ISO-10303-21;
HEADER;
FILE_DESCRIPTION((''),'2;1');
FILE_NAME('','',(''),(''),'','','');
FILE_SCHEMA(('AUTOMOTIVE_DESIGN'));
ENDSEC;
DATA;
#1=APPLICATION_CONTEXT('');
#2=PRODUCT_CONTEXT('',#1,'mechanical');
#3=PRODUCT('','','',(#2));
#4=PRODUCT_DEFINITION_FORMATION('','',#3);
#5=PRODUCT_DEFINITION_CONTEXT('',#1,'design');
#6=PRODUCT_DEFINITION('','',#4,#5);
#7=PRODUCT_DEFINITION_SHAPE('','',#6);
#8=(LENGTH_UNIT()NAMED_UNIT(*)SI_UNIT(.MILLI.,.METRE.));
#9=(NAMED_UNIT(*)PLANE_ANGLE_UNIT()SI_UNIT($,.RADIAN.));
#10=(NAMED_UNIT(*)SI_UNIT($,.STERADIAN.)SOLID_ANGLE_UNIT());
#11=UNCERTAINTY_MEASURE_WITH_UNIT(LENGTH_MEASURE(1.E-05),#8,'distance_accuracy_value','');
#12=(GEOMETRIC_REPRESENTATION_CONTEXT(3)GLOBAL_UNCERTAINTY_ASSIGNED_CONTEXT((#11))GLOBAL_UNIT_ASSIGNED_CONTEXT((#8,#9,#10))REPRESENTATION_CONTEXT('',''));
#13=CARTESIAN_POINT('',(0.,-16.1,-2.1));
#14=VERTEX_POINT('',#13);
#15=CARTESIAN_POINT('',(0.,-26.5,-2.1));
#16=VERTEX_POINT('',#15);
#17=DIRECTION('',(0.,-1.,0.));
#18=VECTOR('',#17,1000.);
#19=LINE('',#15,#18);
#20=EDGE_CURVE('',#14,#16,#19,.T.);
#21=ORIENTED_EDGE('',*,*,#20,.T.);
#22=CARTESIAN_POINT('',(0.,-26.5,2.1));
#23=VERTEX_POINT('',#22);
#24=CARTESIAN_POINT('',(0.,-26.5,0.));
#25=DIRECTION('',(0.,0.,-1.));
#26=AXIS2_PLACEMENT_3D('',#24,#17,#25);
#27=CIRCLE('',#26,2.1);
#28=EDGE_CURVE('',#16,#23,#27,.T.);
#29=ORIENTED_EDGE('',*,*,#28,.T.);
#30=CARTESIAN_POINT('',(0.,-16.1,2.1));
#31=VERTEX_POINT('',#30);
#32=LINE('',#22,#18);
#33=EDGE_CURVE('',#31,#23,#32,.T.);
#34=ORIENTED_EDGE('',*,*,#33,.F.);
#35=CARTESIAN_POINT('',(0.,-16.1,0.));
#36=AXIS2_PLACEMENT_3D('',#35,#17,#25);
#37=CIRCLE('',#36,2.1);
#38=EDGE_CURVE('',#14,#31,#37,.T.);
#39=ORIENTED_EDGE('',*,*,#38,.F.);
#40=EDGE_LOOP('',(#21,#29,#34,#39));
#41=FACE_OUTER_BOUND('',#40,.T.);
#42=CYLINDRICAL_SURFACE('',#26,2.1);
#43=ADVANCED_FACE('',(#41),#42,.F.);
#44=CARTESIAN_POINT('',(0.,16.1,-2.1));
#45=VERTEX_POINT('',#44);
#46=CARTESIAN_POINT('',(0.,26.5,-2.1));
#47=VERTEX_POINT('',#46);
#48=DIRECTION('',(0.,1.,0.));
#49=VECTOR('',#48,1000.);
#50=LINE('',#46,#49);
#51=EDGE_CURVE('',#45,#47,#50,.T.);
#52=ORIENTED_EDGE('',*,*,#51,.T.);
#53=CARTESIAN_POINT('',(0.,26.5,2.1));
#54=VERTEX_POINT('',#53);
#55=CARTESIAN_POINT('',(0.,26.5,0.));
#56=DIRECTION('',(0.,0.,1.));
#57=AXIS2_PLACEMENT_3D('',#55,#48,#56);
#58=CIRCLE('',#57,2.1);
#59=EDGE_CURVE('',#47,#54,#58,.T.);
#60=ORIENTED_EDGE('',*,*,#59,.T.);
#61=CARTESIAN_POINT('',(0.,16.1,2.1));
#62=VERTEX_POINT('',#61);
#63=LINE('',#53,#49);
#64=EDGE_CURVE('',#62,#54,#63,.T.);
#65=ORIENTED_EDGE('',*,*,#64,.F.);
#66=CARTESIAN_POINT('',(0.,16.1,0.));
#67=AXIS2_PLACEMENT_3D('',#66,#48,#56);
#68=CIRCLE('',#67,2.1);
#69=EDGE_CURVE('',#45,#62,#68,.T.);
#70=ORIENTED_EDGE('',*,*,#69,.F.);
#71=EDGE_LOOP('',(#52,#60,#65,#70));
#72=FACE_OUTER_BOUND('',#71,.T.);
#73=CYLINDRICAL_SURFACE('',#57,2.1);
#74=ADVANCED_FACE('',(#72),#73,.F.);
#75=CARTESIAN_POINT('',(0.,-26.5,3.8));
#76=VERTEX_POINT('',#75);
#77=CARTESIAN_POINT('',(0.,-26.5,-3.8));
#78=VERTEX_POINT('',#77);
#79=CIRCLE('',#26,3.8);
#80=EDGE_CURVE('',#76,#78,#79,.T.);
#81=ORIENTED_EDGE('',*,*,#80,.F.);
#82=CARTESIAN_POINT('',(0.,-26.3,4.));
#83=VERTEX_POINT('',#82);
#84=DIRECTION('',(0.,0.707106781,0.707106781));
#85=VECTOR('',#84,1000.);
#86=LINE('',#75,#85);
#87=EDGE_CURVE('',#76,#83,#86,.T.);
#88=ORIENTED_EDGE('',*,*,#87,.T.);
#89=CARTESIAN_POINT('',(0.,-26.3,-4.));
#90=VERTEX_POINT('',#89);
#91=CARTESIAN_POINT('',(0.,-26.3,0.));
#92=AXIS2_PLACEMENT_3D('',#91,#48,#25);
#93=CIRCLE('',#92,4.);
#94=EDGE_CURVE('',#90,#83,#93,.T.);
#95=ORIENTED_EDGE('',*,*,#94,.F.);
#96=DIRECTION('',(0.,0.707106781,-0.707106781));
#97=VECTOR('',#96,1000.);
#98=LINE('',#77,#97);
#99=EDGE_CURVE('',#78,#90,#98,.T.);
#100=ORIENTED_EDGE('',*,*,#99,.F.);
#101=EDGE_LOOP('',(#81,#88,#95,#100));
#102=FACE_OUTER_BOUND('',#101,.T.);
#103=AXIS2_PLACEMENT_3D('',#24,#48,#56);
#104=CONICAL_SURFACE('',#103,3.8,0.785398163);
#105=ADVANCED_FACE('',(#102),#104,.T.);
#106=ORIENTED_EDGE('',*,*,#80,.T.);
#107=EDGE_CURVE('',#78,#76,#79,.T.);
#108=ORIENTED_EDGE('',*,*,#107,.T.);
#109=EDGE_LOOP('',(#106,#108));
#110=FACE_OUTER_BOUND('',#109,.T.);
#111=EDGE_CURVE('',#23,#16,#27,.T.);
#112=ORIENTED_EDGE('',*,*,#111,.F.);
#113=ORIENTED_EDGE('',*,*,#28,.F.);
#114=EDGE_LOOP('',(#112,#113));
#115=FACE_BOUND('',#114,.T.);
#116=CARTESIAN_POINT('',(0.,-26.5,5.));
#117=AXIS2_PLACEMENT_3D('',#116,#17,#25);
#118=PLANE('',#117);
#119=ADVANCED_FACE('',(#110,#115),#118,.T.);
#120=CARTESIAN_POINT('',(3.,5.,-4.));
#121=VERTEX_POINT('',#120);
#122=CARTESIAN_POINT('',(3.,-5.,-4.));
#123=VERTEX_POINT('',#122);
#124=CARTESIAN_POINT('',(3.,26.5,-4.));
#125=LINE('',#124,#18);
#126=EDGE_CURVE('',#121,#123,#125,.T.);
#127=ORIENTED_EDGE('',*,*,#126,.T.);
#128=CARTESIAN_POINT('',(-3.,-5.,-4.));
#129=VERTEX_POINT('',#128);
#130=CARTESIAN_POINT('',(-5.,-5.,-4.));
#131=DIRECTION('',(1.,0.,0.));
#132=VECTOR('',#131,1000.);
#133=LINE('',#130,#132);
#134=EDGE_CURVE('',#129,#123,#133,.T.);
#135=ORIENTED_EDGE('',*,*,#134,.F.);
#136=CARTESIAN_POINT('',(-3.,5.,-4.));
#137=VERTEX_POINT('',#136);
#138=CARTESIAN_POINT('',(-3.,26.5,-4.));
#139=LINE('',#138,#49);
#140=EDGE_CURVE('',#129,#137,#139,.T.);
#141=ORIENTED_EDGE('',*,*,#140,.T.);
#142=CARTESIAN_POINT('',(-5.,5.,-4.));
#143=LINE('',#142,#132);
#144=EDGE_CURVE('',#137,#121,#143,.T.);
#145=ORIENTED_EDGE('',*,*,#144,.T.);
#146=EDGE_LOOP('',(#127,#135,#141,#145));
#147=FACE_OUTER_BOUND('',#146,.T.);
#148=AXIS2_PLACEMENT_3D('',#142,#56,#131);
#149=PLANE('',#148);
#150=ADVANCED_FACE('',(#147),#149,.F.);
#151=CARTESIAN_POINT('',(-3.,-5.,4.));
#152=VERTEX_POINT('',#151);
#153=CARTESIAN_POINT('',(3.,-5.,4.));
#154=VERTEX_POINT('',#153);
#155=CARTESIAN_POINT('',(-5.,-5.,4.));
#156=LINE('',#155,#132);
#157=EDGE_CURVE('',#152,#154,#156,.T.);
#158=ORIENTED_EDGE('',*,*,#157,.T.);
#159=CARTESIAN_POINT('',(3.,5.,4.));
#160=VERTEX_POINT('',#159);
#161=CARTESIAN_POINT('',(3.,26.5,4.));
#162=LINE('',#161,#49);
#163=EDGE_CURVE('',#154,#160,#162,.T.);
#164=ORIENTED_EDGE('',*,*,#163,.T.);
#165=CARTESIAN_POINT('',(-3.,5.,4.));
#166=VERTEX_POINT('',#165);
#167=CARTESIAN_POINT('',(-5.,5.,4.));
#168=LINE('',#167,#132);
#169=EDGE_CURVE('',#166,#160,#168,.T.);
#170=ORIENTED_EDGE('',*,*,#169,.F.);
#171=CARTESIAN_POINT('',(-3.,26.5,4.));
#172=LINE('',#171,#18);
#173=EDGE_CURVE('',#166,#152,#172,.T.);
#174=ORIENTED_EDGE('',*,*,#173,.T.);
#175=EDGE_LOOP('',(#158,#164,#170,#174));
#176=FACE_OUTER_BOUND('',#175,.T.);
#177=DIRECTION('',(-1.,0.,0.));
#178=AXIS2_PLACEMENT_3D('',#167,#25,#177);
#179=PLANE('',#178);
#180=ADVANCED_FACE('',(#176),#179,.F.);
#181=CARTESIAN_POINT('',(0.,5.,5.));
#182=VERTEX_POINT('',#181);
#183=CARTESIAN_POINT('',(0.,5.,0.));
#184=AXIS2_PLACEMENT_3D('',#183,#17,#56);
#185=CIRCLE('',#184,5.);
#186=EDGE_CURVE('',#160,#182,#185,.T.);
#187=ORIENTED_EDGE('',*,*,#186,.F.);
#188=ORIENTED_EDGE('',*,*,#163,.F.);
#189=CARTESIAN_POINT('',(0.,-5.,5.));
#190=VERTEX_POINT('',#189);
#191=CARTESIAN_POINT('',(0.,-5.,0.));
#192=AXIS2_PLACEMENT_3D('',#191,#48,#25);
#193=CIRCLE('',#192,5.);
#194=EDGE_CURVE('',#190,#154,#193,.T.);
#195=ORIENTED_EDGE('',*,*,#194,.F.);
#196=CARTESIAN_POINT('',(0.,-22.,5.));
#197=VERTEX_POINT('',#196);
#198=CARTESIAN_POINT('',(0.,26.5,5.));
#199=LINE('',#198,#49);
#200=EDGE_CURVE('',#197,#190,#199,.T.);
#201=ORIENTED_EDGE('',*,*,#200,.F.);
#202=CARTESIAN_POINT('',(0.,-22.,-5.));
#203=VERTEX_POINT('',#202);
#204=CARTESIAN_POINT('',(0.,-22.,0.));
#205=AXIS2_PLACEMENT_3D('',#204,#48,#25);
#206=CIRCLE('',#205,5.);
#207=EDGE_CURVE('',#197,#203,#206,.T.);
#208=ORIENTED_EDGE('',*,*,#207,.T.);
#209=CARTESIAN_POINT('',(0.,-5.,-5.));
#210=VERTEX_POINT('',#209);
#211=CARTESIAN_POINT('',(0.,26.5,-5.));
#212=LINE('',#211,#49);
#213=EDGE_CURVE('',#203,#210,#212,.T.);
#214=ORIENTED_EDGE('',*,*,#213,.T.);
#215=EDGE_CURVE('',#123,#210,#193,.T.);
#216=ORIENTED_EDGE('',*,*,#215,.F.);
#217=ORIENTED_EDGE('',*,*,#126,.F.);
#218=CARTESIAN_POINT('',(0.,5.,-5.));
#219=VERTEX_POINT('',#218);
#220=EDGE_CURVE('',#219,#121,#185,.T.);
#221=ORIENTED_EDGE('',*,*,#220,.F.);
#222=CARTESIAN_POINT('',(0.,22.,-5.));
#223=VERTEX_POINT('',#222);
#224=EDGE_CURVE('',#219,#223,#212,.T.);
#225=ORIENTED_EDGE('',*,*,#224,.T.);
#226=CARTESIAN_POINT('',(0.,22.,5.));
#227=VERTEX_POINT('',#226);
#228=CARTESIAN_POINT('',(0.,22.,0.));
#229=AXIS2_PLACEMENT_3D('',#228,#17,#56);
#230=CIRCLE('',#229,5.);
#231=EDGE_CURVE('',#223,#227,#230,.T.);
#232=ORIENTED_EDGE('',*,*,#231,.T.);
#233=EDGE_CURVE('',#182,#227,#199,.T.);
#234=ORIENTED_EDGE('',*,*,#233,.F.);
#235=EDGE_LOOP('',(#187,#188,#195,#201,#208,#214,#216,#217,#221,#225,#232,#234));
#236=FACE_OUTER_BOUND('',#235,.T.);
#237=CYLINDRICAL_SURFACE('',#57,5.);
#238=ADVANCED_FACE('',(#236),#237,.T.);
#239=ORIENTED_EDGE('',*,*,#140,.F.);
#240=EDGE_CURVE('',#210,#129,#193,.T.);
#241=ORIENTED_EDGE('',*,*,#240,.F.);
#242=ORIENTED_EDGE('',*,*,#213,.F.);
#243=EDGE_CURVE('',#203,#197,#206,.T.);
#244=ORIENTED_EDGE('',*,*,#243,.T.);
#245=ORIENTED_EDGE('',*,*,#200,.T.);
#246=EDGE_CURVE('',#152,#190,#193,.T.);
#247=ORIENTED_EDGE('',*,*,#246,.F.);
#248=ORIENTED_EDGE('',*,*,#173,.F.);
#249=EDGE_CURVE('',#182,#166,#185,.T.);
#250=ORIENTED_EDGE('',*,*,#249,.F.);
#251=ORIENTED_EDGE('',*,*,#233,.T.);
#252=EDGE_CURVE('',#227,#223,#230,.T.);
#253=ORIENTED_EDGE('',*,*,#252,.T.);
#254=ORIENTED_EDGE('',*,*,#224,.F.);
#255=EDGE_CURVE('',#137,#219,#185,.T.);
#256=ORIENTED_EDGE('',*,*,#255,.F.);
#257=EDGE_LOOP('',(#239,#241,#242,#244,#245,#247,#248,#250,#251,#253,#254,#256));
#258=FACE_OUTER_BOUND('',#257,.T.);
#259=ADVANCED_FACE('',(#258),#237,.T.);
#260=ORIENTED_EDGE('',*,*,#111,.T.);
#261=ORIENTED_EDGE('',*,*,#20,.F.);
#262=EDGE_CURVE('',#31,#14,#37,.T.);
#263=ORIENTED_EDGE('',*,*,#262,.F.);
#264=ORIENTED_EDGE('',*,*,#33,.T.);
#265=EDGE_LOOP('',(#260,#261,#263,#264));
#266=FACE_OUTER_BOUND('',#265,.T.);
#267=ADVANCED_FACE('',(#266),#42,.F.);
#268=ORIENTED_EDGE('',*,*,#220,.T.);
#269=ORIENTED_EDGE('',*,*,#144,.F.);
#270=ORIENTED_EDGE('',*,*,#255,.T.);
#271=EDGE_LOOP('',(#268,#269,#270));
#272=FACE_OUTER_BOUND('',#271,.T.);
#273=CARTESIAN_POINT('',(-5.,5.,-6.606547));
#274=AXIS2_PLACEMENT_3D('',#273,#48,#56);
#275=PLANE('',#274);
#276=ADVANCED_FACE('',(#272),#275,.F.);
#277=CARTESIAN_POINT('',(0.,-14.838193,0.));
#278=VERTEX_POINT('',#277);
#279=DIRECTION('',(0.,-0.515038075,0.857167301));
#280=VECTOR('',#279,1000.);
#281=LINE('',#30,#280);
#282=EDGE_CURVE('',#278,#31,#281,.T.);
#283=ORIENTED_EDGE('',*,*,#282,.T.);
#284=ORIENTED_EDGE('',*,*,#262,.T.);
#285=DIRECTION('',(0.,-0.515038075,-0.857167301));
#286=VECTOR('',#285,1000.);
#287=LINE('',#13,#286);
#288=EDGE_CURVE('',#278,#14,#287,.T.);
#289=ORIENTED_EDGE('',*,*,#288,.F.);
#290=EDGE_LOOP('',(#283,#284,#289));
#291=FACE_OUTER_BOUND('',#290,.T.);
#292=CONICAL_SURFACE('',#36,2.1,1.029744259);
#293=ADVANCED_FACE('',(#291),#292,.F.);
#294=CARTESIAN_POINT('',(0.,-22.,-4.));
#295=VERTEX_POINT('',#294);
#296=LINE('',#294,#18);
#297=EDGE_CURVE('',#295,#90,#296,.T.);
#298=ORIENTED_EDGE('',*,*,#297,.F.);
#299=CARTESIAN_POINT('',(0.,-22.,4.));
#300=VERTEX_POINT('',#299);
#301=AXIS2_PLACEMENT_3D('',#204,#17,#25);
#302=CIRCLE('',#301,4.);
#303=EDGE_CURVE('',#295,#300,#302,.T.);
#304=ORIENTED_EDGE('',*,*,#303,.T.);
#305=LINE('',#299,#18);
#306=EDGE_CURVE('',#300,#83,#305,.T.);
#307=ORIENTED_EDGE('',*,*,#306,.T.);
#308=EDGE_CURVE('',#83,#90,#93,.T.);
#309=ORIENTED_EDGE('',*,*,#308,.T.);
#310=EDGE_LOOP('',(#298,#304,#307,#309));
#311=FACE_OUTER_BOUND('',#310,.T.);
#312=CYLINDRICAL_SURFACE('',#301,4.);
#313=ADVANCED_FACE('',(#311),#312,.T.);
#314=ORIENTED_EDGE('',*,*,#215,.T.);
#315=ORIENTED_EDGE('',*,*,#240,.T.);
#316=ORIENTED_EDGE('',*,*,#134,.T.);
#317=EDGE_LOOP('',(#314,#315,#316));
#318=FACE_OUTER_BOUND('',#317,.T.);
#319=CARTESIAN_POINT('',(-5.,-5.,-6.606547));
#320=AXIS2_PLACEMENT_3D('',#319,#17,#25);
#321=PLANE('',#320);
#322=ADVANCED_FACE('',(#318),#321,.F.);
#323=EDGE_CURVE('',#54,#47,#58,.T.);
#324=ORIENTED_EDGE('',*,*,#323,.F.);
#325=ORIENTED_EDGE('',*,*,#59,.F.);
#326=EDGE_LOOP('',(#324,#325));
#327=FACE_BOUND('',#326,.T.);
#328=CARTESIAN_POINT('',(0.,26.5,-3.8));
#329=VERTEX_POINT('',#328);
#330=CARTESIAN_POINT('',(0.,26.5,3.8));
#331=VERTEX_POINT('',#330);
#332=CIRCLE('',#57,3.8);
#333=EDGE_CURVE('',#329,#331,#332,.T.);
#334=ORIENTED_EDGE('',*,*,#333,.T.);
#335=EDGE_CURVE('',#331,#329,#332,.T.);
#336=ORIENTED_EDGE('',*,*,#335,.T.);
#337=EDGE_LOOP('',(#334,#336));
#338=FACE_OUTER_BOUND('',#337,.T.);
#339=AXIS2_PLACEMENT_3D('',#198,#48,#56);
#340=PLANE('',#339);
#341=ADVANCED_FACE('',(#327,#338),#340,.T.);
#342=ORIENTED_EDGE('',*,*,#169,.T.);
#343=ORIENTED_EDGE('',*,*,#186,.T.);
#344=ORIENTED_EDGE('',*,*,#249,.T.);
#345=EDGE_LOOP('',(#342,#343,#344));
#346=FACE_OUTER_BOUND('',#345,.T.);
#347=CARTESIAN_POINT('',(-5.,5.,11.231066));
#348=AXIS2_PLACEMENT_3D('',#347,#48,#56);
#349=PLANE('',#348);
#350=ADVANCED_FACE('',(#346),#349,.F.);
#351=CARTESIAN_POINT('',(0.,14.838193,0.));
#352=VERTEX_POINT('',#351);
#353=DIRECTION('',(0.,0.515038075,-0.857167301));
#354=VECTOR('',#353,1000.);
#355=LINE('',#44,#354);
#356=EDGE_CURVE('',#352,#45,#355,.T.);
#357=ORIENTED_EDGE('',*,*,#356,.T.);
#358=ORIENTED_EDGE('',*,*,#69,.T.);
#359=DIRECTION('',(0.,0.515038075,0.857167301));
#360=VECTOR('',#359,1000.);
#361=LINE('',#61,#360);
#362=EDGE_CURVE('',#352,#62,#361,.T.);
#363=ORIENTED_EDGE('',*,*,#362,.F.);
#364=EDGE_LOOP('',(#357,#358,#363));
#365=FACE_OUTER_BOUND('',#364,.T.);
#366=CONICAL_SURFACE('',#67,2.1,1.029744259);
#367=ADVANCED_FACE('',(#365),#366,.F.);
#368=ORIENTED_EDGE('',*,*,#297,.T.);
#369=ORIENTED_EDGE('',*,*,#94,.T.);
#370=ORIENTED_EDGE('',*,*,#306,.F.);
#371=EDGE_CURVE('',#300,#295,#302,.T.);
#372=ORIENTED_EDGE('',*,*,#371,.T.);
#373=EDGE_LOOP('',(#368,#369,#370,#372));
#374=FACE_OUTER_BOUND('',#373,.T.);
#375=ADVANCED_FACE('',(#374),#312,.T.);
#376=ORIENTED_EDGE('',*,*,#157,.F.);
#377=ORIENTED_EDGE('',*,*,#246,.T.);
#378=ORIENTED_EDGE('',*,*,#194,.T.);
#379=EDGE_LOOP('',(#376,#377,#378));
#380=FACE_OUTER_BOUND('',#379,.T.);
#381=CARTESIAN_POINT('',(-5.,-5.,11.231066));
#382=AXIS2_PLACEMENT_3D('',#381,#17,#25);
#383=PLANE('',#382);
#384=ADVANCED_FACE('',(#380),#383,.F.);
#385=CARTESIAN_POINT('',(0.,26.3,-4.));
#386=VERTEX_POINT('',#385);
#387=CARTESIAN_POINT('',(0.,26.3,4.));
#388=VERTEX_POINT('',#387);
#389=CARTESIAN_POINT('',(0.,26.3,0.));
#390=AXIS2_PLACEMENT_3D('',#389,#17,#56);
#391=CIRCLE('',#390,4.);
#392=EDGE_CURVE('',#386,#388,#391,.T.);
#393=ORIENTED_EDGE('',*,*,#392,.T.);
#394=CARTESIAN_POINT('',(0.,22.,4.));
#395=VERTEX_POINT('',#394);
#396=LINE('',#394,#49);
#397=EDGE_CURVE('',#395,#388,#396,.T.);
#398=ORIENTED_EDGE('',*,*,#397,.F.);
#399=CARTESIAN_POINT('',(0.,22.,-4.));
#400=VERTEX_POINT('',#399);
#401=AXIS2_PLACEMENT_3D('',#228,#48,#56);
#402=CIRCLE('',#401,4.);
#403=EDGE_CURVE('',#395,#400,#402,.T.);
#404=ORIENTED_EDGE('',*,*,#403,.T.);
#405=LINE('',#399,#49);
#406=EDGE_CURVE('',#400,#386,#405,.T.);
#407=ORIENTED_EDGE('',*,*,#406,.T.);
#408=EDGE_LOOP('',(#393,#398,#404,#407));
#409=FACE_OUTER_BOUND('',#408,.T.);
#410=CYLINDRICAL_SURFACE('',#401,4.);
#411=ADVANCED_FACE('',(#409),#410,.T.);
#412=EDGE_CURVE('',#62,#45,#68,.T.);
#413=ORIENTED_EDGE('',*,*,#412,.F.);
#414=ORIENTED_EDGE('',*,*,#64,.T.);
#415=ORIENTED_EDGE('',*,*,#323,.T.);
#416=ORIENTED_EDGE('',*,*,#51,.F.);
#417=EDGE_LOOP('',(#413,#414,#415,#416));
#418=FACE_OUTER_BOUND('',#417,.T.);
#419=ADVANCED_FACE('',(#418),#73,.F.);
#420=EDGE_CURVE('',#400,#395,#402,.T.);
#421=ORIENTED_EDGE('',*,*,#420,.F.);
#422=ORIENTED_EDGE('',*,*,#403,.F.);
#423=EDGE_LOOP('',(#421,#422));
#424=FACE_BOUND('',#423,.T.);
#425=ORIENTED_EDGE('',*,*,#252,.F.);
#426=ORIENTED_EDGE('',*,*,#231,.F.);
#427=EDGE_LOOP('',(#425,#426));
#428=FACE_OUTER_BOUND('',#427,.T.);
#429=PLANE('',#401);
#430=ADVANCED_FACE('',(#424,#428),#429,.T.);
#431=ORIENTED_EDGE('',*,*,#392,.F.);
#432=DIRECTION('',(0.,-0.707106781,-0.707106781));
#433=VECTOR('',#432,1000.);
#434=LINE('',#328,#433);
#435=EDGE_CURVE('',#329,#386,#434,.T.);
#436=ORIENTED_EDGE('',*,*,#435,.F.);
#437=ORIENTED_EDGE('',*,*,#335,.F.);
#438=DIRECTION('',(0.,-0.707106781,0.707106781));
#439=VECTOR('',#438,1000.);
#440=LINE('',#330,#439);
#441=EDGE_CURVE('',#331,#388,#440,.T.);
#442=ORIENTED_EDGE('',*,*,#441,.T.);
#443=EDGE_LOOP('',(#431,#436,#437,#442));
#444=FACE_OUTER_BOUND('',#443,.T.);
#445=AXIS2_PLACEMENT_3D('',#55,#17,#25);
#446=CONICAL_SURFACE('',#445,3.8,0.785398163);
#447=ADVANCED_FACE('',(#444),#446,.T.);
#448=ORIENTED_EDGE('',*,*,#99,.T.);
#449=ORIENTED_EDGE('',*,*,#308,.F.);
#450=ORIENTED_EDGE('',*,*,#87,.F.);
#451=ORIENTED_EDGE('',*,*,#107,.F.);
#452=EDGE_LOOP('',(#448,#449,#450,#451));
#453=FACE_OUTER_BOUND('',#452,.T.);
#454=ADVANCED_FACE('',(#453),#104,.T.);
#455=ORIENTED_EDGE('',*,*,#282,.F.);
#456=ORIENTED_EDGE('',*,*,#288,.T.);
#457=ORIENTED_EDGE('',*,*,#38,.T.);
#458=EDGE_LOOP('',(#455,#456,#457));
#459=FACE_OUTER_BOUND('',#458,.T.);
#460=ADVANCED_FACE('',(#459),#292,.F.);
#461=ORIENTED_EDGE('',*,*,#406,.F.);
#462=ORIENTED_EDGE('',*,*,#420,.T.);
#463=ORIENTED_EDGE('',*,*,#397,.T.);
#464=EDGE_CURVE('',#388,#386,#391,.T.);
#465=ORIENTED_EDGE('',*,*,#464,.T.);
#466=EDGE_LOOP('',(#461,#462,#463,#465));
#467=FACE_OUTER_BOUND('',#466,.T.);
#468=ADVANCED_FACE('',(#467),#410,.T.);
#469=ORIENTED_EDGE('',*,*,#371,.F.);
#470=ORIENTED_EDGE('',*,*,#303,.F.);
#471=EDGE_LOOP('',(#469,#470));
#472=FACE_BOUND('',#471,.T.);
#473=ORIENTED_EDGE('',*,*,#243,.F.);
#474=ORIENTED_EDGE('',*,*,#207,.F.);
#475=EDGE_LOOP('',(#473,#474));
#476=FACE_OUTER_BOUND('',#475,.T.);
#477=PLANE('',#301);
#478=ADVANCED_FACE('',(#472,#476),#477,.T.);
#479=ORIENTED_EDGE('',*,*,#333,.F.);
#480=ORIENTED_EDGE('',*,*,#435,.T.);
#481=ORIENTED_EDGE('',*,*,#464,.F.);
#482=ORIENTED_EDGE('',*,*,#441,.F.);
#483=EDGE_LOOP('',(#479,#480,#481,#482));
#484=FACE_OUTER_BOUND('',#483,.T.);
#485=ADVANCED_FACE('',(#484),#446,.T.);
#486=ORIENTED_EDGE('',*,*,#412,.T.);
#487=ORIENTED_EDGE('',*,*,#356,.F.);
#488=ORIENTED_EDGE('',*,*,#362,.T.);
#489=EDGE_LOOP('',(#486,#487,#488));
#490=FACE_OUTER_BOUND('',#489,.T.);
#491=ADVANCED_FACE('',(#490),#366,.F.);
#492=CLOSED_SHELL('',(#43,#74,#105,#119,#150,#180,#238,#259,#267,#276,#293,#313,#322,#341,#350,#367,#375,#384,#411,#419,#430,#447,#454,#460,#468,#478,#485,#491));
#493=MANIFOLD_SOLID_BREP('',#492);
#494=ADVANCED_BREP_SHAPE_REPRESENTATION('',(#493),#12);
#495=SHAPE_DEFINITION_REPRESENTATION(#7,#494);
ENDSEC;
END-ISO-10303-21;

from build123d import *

# Parameters (mm, degrees)
SKETCH1_W           = 5
SKETCH1_H           = 53
SKETCH4_OUTSIDE_W   = 22.97
SKETCH4_OUTSIDE_H   = 22.97
SKETCH4_OUTSIDE_R   = 4
EXTRUDE1_DEPTH      = 4.5
SKETCH5_OUTSIDE_W   = 22.97
SKETCH5_OUTSIDE_H   = 22.97
SKETCH5_OUTSIDE_R   = 4
EXTRUDE2_DEPTH      = 4.5
EXTRUDE3_DEPTH      = 28.427176304
EXTRUDE3_DEPTH_BACK = 28.427176304
SKETCH6_W           = 7.231066263
SKETCH6_H           = 10
SKETCH6_W_2         = 2.606547141
CHAMFER1_SIZE       = 0.2


with BuildPart() as part:
    # Sketch1 → Revolve1 (revolve)
    with BuildSketch(Plane(origin=(0, 0, 0), x_dir=(0, 0, -1), z_dir=(1, 0, 0))):
        with Locations((-2.5, 0)):
            Rectangle(SKETCH1_W, SKETCH1_H)
    revolve(axis=Axis((0, 26.5, 0), (0, -1, 0)))

    # Sketch2 → M5 Tapped Hole1 (revolve, cut)
    with BuildSketch(Plane(origin=(0, 26.5, 0), x_dir=(0, 0, 1), z_dir=(1, 0, 0))):
        Polygon((0, 0), (0, 11.6618073), (2.1, 10.4), (2.1, 0), align=None)
    m5_tapped_hole1 = revolve(axis=Axis((0, 32.85, 0), (0, -1, 0)), mode=Mode.SUBTRACT)

    # Mirror1: M5 Tapped Hole1 across plane
    add(m5_tapped_hole1.mirror(Plane.ZX), mode=Mode.SUBTRACT)

    # Sketch4 outside → Extrude1 (cut)
    with BuildSketch(Plane.XZ.offset(26.5)):
        Rectangle(SKETCH4_OUTSIDE_W, SKETCH4_OUTSIDE_H)
        with Locations(Location((0, 0, 0), (0, 0, 270))):
            Circle(SKETCH4_OUTSIDE_R, mode=Mode.SUBTRACT)
    extrude(amount=-EXTRUDE1_DEPTH, mode=Mode.SUBTRACT)

    # Sketch5 outside → Extrude2 (cut)
    with BuildSketch(Plane(origin=(0, 26.5, 0), x_dir=(1, 0, 0), z_dir=(0, 1, 0))):
        Rectangle(SKETCH5_OUTSIDE_W, SKETCH5_OUTSIDE_H)
        with Locations(Location((0, 0, 0), (0, 0, 90))):
            Circle(SKETCH5_OUTSIDE_R, mode=Mode.SUBTRACT)
    extrude(amount=-EXTRUDE2_DEPTH, mode=Mode.SUBTRACT)

    # Sketch6 → Extrude3 (cut, two sides: drawn at the far end of the back side and taken through both)
    with BuildSketch(Plane(origin=(0, 0, 0), x_dir=(0, 0, -1), z_dir=(1, 0, 0)).offset(-EXTRUDE3_DEPTH_BACK)):
        with Locations((-7.615533132, 0)):
            Rectangle(SKETCH6_W, SKETCH6_H)
        with Locations((5.303273571, 0)):
            Rectangle(SKETCH6_W_2, SKETCH6_H)
    extrude(amount=EXTRUDE3_DEPTH + EXTRUDE3_DEPTH_BACK, mode=Mode.SUBTRACT)

    # Chamfer1
    chamfer1_edges = [part.edges().sort_by_distance(p)[0] for p in [
        (0, -26.5, 4),
        (0, 26.5, 4),
    ]]
    chamfer(chamfer1_edges, length=CHAMFER1_SIZE)


solid = part.part
